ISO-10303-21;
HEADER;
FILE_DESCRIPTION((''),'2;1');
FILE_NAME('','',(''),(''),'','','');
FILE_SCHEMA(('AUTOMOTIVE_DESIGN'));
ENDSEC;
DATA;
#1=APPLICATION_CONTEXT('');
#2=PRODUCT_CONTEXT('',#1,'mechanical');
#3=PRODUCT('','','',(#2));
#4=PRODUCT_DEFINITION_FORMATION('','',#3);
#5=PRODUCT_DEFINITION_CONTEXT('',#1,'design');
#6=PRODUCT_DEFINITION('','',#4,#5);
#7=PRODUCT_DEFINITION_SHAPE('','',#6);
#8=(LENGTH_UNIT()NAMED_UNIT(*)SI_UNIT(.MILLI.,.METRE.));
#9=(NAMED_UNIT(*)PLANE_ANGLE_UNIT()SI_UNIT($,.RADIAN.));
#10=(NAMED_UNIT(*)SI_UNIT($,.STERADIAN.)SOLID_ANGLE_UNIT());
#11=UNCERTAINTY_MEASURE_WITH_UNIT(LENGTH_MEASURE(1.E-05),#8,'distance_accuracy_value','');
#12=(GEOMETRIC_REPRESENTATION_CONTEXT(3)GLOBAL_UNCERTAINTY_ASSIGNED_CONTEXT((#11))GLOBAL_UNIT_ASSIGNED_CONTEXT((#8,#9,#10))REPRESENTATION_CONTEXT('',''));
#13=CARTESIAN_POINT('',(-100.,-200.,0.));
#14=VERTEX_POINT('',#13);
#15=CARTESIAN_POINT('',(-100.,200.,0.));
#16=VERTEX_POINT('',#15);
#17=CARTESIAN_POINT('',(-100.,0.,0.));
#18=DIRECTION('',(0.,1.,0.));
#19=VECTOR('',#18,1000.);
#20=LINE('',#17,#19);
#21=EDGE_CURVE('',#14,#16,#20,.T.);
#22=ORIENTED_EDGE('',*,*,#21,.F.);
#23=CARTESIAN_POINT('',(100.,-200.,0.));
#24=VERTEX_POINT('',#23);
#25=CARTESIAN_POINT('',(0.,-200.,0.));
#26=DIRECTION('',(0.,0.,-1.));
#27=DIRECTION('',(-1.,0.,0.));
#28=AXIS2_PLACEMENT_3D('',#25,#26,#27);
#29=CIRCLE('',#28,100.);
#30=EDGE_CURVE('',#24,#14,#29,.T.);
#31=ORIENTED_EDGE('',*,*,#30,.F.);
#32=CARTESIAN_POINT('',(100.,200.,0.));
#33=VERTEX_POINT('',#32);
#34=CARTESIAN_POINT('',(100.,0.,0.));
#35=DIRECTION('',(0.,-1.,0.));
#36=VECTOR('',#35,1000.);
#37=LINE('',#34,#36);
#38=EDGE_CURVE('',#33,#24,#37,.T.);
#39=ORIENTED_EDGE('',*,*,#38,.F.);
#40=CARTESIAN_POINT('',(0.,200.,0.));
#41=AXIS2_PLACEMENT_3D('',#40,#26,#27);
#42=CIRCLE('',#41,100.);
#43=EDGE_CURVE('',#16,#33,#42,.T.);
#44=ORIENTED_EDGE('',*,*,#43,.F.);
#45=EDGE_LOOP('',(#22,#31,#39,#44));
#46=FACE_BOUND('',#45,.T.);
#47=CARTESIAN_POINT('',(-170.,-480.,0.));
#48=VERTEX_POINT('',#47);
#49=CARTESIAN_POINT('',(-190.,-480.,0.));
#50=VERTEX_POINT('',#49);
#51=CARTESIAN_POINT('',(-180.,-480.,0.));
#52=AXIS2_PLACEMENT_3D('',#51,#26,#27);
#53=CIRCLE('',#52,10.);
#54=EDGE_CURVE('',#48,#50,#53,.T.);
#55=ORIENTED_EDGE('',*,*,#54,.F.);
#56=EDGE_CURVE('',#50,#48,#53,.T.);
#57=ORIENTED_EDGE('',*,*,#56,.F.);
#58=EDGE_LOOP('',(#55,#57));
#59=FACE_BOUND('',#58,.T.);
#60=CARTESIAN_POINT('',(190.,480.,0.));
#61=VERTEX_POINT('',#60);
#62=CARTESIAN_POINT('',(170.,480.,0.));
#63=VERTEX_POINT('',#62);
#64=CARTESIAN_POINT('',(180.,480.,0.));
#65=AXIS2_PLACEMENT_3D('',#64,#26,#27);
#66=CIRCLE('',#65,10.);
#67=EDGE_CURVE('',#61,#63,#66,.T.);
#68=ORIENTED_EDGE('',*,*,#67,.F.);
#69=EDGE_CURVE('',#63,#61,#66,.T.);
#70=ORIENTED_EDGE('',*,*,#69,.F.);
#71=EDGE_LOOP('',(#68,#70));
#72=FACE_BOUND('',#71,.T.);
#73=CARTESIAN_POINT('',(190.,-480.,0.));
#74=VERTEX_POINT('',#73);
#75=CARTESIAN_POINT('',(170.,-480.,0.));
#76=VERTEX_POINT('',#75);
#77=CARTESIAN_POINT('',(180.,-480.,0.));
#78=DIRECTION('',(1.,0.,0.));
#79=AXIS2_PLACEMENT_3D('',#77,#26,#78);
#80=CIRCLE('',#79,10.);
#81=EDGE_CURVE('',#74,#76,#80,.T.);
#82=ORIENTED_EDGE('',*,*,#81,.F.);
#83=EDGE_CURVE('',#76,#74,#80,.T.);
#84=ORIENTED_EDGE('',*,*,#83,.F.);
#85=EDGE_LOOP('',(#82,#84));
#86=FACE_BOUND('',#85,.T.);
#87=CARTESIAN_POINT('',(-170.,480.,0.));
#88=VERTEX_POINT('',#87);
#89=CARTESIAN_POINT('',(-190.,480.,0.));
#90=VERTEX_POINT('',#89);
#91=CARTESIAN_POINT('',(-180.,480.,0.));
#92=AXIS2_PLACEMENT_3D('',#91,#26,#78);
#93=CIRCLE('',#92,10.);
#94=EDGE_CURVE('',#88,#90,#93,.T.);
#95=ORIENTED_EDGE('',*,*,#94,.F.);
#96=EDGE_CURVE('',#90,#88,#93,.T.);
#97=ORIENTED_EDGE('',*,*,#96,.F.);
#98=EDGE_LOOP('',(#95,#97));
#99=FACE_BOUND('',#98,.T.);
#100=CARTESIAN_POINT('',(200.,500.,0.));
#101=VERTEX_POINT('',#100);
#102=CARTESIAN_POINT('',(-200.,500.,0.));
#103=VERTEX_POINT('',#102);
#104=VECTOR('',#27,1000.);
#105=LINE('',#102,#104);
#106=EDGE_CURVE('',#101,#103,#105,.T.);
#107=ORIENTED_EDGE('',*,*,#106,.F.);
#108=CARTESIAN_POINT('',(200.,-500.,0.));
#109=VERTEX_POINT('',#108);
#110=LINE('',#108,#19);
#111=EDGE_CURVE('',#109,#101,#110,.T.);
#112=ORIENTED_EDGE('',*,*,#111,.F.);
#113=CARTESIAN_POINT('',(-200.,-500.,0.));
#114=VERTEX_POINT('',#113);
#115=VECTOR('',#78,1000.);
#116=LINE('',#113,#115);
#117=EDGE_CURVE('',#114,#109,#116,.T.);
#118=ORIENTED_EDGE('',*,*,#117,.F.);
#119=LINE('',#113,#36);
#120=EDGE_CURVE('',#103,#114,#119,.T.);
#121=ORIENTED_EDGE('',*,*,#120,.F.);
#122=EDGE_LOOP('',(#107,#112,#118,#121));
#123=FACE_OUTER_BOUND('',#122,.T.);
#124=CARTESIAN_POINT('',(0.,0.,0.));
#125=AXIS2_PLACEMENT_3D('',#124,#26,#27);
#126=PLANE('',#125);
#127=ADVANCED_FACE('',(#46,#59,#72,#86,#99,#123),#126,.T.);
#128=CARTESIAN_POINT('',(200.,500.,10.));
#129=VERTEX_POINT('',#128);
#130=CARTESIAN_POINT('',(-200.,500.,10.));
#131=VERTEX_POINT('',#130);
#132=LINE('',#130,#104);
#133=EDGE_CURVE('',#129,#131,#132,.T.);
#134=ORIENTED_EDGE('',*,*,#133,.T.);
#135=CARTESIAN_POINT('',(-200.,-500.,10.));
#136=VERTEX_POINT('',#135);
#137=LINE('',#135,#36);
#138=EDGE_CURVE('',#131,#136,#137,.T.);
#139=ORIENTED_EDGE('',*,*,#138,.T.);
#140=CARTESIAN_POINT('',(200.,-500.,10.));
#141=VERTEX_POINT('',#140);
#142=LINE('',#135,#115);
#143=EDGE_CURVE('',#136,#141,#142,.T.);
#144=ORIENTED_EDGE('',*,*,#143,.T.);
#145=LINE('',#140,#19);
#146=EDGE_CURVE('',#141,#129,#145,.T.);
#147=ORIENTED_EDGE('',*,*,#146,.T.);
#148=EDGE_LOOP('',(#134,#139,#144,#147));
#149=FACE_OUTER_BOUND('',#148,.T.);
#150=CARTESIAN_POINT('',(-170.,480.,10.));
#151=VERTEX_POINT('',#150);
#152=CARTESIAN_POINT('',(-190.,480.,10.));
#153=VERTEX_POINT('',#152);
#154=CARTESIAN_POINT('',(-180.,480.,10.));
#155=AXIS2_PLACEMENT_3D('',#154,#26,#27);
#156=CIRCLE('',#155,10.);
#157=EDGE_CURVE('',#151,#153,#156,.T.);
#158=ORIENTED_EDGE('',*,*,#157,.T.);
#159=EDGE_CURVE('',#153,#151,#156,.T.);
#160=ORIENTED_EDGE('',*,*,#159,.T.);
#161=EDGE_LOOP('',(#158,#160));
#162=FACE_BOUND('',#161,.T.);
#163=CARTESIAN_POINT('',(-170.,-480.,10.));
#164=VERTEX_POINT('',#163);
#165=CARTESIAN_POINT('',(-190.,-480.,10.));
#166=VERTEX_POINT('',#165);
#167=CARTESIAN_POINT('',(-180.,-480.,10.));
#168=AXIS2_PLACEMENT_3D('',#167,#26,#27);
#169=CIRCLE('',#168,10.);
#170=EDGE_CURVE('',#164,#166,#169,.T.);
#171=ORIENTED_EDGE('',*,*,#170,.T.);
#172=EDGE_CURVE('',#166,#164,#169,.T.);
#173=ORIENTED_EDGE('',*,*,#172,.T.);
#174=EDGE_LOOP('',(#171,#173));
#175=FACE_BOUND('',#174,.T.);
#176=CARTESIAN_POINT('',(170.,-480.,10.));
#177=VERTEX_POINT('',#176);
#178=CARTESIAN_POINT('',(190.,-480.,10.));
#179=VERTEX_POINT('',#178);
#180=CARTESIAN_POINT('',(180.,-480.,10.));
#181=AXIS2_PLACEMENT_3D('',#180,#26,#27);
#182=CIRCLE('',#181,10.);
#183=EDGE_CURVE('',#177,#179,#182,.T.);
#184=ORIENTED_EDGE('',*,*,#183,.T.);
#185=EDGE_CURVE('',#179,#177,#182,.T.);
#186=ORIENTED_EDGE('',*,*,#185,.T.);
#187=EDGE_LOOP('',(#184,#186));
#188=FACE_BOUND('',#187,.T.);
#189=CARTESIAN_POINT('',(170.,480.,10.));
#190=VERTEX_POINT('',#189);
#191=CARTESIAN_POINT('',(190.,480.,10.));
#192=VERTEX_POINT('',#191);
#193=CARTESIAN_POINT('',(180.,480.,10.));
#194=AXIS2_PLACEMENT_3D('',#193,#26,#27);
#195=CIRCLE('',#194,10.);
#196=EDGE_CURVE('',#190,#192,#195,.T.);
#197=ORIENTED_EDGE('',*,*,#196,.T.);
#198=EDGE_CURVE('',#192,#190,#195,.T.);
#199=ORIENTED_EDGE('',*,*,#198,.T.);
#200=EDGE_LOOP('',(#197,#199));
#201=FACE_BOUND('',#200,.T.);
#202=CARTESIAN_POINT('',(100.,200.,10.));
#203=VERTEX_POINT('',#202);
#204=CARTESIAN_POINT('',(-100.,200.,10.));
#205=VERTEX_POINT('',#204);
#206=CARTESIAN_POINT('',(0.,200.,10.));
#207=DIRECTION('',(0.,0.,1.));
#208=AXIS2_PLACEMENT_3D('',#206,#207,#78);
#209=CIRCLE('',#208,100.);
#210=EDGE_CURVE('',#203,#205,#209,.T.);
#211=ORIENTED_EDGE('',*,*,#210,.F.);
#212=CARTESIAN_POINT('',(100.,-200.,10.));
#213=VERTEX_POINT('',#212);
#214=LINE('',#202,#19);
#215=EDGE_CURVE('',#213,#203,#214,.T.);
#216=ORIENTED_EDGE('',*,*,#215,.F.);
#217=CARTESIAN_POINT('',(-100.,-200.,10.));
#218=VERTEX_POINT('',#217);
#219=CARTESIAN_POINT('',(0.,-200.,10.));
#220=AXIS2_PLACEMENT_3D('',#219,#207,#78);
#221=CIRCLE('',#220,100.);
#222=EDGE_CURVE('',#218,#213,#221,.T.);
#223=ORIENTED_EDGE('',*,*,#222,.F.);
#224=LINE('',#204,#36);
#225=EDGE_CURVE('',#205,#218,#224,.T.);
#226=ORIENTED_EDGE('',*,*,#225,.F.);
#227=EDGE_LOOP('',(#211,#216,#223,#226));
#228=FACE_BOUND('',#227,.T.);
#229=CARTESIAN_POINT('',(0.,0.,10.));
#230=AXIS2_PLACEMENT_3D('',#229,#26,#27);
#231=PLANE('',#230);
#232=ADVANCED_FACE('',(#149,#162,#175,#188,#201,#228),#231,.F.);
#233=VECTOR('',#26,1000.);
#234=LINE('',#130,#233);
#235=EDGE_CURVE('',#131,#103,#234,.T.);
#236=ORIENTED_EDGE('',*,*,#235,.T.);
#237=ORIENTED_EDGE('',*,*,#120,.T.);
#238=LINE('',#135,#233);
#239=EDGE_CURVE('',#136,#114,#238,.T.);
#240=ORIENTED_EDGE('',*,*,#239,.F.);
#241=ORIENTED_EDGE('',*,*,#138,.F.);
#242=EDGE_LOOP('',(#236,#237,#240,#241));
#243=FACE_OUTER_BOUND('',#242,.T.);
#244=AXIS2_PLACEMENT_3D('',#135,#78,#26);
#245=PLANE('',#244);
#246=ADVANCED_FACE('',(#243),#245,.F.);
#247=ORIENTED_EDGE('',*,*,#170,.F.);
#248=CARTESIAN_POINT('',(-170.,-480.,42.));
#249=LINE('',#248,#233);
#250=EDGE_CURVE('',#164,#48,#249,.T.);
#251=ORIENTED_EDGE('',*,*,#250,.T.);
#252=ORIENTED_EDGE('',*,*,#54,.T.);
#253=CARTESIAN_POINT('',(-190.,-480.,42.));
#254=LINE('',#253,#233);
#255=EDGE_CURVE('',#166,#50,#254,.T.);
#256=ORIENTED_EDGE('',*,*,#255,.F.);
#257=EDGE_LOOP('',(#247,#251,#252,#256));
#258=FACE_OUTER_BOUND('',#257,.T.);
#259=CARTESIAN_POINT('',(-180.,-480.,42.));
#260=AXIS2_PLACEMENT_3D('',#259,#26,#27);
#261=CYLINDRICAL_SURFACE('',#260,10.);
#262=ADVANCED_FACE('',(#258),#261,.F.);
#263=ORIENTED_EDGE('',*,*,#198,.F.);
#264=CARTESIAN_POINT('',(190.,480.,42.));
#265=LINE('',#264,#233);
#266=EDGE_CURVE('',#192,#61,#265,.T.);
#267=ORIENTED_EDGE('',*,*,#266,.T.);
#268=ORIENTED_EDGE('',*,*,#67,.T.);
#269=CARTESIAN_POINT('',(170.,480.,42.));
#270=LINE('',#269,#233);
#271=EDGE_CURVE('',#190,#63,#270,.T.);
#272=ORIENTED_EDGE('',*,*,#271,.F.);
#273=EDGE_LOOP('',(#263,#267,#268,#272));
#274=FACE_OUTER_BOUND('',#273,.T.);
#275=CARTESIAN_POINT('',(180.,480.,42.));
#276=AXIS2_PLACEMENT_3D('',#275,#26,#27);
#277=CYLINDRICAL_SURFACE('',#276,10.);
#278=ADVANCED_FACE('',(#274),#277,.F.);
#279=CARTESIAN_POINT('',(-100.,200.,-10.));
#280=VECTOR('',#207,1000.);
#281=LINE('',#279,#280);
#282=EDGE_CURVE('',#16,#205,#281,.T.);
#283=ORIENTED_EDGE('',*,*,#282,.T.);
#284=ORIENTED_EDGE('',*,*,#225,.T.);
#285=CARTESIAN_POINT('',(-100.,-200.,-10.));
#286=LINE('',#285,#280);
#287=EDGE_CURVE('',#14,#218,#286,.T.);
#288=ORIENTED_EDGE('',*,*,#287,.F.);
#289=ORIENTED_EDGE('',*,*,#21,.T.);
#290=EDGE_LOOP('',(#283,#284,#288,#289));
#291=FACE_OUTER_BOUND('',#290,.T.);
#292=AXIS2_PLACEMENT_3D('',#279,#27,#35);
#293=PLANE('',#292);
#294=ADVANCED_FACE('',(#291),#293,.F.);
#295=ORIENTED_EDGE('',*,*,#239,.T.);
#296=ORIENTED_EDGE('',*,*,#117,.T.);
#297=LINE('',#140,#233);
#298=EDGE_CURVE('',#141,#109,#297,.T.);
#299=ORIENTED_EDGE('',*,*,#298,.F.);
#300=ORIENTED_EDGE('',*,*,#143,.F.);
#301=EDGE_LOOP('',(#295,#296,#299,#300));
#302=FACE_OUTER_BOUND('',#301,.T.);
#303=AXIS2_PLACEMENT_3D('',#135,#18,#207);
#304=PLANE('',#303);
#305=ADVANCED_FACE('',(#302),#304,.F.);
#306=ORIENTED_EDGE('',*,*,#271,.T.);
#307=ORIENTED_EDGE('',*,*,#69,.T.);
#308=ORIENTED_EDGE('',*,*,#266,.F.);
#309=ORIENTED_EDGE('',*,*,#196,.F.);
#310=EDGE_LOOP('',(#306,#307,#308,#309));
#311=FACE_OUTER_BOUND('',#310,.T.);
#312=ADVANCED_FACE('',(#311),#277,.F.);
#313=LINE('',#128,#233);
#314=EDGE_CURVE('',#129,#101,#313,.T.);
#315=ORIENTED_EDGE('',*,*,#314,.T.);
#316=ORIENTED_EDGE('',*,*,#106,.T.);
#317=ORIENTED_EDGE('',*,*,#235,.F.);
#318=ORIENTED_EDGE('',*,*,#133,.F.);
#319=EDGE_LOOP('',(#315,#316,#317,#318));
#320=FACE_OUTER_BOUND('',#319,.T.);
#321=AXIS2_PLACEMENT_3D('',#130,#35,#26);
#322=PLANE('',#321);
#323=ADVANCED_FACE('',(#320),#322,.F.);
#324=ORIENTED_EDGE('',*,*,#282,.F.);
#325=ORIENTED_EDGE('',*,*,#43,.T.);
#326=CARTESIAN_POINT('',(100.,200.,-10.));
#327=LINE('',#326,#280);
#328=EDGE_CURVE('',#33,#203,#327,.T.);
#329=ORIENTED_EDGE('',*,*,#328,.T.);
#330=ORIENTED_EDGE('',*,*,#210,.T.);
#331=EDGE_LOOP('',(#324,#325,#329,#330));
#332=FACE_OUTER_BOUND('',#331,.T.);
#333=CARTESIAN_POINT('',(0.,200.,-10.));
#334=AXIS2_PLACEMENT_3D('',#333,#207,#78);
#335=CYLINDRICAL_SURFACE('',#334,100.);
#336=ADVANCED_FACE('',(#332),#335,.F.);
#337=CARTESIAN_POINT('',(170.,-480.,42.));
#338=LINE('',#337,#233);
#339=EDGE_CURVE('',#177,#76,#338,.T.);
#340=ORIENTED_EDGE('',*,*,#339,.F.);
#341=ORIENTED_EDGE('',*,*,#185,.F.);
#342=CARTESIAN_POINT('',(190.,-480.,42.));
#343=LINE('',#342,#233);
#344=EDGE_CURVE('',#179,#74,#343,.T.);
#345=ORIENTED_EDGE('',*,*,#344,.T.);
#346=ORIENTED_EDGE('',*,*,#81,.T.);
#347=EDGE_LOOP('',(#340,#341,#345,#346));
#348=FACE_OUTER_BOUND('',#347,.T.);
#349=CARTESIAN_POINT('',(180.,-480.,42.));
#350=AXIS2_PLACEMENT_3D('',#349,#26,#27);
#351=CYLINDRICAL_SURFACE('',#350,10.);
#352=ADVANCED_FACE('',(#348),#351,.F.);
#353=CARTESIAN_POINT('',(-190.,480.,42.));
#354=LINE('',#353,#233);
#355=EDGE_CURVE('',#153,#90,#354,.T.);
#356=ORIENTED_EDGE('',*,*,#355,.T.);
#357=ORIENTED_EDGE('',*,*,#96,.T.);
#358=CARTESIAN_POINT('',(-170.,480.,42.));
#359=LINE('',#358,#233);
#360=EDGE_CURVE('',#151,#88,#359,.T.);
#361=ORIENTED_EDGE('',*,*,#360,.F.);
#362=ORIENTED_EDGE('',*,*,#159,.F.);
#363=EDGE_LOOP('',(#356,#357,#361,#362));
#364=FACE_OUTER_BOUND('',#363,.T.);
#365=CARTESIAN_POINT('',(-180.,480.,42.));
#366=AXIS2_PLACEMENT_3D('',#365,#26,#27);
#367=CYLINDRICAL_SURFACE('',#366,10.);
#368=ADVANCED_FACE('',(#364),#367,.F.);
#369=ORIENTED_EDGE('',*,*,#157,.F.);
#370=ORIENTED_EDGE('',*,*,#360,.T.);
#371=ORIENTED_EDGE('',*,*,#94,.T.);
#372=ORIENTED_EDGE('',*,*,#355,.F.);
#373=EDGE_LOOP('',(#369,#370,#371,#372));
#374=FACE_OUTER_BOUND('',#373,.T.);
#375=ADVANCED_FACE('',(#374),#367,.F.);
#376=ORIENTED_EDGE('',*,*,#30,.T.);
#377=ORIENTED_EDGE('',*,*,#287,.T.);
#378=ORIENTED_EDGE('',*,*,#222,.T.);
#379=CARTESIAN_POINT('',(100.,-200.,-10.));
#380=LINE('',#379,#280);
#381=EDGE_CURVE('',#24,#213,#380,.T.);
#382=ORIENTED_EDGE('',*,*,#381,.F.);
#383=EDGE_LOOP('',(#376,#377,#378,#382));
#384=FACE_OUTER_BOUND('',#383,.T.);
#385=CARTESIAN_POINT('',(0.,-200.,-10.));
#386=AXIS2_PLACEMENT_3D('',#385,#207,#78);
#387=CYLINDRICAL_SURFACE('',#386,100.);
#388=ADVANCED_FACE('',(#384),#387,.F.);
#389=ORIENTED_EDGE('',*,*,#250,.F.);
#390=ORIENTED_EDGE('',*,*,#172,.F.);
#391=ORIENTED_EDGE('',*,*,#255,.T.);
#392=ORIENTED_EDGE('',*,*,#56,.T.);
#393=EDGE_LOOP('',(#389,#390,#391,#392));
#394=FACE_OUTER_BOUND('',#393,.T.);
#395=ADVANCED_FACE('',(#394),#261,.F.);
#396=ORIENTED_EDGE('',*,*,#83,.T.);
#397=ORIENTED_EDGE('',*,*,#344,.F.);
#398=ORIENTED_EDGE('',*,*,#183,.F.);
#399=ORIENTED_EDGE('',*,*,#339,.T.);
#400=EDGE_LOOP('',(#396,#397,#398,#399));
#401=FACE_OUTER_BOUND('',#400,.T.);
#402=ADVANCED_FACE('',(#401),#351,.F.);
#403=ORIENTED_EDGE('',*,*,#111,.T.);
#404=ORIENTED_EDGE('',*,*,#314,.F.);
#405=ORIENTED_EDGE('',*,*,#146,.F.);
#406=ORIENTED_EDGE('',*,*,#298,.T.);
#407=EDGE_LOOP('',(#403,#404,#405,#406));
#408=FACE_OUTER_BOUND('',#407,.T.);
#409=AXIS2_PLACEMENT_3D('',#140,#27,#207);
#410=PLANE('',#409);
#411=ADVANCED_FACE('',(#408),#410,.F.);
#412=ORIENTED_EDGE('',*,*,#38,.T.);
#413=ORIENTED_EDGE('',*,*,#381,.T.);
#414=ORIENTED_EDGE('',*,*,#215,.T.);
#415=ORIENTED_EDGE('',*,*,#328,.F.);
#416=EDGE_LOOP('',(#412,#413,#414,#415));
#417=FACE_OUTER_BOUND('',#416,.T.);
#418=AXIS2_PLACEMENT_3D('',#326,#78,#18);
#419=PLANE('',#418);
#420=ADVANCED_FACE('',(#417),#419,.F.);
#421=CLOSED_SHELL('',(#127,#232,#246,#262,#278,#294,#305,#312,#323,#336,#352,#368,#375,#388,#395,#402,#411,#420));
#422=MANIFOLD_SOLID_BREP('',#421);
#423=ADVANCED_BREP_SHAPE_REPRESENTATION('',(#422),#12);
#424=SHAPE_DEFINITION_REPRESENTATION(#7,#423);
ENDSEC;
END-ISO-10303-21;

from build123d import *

# Parameters (mm, degrees)
SKETCH1_W           = 400
SKETCH1_H           = 1000
BOSS_EXTRUDE1_DEPTH = 10
SKETCH2_R           = 10
CUT_EXTRUDE1_DEPTH  = 42
CUT_EXTRUDE2_DEPTH  = 20


with BuildPart() as part:
    # Sketch1 → Boss-Extrude1 (new body)
    with BuildSketch(Plane.XY):
        Rectangle(SKETCH1_W, SKETCH1_H)
    extrude(amount=BOSS_EXTRUDE1_DEPTH)

    # Sketch2 → Cut-Extrude1 (cut)
    with BuildSketch(Plane(origin=(0, 0, 0), x_dir=(-1, 0, 0), z_dir=(0, 0, -1))):
        with Locations((-180, 480)):
            Circle(SKETCH2_R)
        with Locations((180, 480)):
            Circle(SKETCH2_R)
        with Locations((180, -480)):
            Circle(SKETCH2_R)
        with Locations((-180, -480)):
            Circle(SKETCH2_R)
    extrude(amount=-CUT_EXTRUDE1_DEPTH, mode=Mode.SUBTRACT)

    # Sketch3 → Cut-Extrude2 (cut)
    with BuildSketch(Plane.XY.offset(10)):
        with BuildLine():
            Line((100, 200), (100, -200))
            ThreePointArc((100, -200), (0, -300), (-100, -200))
            Line((-100, -200), (-100, 200))
            ThreePointArc((-100, 200), (0, 300), (100, 200))
        make_face()
    extrude(amount=-CUT_EXTRUDE2_DEPTH, mode=Mode.SUBTRACT)


solid = part.part
